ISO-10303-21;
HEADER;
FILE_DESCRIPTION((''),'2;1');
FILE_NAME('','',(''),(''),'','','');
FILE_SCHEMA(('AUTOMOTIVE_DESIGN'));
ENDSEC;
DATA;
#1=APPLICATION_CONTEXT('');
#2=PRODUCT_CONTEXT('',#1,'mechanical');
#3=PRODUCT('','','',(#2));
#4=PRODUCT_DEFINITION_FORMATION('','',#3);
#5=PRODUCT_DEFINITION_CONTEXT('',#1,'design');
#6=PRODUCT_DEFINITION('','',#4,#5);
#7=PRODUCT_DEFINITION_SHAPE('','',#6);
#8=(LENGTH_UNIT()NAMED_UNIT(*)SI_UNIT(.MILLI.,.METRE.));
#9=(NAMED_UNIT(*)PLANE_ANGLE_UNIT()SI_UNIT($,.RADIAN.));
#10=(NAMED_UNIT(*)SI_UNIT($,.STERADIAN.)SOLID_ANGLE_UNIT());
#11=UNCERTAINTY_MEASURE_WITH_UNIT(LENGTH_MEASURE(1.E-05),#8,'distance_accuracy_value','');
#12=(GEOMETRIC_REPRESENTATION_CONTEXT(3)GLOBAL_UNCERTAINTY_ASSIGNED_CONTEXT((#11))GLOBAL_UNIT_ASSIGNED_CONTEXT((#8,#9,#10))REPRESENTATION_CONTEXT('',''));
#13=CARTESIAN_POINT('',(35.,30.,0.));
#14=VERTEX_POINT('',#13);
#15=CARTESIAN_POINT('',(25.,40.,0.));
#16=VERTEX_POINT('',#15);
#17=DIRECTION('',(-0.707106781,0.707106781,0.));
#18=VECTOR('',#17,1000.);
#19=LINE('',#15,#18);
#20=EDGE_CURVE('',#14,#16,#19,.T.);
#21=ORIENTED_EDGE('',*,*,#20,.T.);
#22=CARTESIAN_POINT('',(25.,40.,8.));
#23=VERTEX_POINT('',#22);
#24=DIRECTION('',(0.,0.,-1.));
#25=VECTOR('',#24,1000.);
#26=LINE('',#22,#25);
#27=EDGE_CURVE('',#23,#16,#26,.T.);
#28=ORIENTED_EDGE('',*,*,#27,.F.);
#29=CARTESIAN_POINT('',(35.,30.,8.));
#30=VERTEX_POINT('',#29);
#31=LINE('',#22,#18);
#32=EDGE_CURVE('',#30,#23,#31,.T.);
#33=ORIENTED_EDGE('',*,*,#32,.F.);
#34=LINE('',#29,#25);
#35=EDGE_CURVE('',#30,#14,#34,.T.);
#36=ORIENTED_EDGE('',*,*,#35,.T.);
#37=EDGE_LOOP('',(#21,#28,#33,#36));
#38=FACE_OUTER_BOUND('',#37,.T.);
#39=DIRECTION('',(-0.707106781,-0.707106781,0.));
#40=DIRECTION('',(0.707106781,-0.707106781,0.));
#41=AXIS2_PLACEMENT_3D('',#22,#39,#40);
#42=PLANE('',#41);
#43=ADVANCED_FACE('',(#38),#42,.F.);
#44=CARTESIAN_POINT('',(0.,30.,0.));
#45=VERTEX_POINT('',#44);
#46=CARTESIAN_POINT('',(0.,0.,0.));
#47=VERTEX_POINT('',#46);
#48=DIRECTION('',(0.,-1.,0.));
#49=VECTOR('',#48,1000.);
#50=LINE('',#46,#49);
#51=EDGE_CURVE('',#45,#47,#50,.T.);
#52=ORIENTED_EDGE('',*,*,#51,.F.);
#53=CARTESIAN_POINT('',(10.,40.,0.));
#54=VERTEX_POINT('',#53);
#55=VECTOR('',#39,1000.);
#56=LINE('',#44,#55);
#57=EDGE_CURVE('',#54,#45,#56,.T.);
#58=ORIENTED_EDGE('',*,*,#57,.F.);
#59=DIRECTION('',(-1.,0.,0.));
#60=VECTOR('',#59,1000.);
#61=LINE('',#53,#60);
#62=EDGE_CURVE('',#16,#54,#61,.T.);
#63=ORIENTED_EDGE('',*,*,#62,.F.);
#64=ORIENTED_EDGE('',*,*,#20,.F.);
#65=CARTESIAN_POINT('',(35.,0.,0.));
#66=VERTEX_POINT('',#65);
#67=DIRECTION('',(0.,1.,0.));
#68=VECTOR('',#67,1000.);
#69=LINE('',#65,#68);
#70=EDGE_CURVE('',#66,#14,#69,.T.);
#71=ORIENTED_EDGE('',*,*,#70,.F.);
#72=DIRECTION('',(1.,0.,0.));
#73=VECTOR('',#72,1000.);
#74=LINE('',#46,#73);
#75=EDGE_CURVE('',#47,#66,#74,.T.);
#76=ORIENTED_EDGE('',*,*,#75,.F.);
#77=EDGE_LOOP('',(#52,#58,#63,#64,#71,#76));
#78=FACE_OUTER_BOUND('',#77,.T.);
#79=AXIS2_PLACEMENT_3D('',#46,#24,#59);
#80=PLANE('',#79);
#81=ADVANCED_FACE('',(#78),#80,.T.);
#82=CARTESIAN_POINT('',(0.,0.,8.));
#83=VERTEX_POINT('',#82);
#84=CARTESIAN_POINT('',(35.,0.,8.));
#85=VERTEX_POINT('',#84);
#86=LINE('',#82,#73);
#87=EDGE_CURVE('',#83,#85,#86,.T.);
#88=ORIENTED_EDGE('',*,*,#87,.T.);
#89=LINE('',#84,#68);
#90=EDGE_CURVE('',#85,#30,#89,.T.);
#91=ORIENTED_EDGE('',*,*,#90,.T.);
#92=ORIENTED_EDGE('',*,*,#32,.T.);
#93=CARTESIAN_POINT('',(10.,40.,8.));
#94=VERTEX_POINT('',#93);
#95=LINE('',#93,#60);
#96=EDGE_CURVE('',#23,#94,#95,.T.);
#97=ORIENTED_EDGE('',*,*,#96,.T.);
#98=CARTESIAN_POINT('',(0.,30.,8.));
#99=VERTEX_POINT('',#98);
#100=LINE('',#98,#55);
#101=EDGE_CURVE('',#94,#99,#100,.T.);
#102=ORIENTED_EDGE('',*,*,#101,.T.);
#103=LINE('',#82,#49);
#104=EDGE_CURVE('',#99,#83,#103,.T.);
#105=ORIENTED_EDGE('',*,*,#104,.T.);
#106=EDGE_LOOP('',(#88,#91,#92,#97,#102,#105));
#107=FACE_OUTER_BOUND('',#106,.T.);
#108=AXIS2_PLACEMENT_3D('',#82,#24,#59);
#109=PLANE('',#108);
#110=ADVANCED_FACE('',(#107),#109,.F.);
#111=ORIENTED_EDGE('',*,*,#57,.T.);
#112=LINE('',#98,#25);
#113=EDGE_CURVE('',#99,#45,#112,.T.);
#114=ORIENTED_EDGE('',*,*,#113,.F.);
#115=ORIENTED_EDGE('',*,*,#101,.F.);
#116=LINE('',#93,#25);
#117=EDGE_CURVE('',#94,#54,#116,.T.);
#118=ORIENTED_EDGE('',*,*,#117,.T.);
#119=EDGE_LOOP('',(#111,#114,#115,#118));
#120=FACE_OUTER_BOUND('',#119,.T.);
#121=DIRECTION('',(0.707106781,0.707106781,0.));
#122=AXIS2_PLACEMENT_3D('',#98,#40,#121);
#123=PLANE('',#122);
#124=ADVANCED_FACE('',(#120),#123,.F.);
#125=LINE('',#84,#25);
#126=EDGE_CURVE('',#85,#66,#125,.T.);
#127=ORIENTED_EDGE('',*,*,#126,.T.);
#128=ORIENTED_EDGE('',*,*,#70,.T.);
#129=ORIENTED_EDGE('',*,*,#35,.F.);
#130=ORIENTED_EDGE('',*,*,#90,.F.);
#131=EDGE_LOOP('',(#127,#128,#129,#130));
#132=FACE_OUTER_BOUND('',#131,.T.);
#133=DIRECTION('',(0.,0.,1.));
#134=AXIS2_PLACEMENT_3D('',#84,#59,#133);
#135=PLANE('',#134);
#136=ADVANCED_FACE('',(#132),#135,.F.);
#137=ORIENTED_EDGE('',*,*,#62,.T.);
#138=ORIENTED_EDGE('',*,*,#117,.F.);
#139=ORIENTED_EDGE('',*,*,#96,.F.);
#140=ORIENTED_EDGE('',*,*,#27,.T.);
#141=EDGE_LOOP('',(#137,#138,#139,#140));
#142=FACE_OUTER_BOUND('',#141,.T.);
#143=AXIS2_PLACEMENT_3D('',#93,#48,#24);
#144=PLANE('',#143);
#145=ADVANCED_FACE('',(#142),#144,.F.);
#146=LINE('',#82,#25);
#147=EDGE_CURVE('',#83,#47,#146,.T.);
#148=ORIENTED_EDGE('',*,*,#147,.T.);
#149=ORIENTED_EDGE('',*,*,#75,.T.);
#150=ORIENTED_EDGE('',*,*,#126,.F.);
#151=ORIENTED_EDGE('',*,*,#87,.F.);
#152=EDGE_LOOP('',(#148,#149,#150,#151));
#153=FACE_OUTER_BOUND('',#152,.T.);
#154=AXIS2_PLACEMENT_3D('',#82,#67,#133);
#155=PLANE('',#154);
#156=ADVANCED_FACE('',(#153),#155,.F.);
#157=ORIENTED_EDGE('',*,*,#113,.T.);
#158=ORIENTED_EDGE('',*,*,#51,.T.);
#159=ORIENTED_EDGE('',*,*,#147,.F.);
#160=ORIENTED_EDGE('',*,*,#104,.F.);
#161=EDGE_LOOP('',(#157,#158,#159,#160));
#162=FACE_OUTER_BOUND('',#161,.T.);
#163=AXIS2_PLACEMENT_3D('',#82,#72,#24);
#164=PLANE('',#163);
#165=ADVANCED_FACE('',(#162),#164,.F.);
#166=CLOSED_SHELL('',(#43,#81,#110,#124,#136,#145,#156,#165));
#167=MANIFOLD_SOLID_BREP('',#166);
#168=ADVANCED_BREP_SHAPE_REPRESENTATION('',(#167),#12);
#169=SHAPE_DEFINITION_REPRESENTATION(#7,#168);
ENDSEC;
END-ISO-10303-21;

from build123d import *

# Parameters (mm, degrees)
BOSS_EXTRUDE1_DEPTH = 8


with BuildPart() as part:
    # Sketch1 → Boss-Extrude1 (new body)
    with BuildSketch(Plane.XY):
        Polygon((0, 30), (10, 40), (25, 40), (35, 30), (35, 0), (0, 0), align=None)
    extrude(amount=BOSS_EXTRUDE1_DEPTH)


solid = part.part
